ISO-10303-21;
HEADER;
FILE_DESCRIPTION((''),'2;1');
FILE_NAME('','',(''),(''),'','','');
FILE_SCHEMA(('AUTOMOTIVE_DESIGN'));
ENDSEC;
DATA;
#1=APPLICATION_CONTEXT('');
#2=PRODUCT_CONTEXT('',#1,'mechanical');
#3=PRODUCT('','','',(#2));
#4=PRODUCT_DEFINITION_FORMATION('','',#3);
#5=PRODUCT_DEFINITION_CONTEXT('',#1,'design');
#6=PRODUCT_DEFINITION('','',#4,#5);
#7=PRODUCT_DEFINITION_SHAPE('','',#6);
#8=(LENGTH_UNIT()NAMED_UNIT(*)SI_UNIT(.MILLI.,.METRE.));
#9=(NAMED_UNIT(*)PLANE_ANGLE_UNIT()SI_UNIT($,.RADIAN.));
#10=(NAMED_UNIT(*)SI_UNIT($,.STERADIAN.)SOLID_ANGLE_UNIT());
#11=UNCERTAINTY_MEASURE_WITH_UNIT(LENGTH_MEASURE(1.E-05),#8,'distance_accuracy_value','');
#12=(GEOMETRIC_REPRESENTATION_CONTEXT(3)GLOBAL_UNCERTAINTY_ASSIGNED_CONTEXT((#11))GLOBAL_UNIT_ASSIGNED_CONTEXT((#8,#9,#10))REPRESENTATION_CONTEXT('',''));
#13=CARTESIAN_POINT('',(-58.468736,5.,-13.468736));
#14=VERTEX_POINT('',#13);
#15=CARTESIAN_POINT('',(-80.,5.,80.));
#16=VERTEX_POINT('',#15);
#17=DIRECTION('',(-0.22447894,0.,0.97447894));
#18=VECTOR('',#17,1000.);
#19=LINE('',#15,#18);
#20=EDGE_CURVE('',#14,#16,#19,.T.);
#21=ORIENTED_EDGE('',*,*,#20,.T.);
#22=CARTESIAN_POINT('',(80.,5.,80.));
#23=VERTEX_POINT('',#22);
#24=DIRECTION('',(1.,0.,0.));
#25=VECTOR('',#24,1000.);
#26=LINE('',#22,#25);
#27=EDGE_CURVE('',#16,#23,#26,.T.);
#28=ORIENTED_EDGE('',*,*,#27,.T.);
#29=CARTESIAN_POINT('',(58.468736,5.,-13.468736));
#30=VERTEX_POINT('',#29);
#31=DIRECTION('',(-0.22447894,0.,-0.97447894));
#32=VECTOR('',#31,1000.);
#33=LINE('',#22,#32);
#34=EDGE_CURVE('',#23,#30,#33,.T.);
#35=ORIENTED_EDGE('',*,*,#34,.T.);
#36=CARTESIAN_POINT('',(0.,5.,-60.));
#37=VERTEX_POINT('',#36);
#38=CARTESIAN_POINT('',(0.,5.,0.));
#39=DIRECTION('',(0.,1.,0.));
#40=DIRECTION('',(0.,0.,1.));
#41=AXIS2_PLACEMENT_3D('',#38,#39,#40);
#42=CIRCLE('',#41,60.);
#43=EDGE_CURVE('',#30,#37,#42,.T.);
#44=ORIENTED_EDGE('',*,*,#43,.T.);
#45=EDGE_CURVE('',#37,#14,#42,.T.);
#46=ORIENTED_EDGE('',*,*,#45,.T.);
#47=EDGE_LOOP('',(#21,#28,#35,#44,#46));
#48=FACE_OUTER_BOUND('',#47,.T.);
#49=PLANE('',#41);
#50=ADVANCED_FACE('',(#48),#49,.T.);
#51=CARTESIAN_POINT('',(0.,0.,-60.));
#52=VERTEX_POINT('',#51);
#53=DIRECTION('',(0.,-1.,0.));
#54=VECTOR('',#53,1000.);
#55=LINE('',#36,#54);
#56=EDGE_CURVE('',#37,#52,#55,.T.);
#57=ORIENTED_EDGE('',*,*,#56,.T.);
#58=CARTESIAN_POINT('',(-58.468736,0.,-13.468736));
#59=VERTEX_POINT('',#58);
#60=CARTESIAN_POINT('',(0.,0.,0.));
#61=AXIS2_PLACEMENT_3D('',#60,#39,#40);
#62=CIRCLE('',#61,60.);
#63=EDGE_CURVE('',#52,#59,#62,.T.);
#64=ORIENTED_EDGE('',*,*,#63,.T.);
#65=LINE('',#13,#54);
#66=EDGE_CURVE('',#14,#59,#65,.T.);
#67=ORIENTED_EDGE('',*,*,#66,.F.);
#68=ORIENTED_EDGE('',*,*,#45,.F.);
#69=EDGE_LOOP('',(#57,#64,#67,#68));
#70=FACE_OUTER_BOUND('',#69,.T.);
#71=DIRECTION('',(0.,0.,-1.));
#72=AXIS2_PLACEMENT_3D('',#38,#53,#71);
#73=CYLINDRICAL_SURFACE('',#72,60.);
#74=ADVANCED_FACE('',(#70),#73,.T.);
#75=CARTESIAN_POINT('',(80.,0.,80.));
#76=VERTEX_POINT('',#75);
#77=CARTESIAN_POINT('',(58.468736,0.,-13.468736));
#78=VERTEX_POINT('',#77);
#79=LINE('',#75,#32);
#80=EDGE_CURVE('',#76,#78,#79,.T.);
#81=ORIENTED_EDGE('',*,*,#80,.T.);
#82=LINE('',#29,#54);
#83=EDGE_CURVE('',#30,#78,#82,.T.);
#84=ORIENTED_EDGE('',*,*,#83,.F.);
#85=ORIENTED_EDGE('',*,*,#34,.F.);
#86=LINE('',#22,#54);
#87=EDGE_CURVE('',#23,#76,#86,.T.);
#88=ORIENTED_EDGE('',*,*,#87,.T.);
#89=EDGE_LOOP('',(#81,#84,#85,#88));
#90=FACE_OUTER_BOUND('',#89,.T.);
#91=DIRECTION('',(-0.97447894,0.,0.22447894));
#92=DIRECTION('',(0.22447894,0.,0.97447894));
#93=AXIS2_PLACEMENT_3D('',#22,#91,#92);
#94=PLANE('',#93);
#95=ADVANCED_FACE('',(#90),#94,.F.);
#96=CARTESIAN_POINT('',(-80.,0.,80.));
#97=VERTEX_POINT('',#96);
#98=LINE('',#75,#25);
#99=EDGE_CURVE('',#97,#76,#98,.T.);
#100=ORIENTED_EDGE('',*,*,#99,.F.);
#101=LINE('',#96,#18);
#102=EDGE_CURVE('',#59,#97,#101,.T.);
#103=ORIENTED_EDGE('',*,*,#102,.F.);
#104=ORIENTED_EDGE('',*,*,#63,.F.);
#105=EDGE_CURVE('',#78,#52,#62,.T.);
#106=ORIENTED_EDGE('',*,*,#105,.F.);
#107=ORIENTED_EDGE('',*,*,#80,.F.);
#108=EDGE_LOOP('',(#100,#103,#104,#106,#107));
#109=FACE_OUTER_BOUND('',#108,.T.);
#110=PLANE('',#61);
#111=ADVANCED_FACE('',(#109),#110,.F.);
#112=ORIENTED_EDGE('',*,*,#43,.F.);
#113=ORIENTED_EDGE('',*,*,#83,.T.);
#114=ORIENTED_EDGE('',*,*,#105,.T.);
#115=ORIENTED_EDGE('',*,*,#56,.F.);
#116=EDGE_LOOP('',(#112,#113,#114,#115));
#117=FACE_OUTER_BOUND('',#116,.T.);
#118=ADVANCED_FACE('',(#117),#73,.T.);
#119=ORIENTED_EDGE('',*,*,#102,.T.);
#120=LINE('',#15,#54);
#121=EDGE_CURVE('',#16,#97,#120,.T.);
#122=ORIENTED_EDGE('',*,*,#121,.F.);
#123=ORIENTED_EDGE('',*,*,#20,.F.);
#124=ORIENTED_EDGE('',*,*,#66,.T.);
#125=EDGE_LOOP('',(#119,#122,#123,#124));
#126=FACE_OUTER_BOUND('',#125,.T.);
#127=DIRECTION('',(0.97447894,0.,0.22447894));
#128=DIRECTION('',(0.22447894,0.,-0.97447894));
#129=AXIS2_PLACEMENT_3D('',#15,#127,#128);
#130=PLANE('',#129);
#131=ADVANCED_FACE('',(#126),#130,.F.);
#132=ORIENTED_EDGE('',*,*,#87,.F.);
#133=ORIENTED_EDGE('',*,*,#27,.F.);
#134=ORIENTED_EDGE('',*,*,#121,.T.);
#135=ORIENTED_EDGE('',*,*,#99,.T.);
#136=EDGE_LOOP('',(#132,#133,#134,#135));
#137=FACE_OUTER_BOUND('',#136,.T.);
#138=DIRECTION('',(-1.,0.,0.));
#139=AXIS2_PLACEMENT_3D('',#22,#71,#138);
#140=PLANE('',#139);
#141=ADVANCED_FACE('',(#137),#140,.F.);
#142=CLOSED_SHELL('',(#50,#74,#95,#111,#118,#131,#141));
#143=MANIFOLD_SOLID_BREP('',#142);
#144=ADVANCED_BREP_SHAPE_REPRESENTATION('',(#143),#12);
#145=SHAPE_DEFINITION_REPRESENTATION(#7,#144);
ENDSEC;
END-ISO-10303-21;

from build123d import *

# Parameters (mm, degrees)
EXTRUDE_1_DEPTH = 5


with BuildPart() as part:
    # 草图1 → 凸台-拉伸1 (new body)
    with BuildSketch(Plane(origin=(0, 0, 0), x_dir=(1, 0, 0), z_dir=(0, 1, 0))):
        with BuildLine():
            Line((80, -80), (-80, -80))
            Line((-80, -80), (-58.468736425, 13.468736425))
            ThreePointArc((-58.468736425, 13.468736425), (0, 60), (58.468736425, 13.468736425))
            Line((58.468736425, 13.468736425), (80, -80))
        make_face()
    extrude(amount=EXTRUDE_1_DEPTH)


solid = part.part
